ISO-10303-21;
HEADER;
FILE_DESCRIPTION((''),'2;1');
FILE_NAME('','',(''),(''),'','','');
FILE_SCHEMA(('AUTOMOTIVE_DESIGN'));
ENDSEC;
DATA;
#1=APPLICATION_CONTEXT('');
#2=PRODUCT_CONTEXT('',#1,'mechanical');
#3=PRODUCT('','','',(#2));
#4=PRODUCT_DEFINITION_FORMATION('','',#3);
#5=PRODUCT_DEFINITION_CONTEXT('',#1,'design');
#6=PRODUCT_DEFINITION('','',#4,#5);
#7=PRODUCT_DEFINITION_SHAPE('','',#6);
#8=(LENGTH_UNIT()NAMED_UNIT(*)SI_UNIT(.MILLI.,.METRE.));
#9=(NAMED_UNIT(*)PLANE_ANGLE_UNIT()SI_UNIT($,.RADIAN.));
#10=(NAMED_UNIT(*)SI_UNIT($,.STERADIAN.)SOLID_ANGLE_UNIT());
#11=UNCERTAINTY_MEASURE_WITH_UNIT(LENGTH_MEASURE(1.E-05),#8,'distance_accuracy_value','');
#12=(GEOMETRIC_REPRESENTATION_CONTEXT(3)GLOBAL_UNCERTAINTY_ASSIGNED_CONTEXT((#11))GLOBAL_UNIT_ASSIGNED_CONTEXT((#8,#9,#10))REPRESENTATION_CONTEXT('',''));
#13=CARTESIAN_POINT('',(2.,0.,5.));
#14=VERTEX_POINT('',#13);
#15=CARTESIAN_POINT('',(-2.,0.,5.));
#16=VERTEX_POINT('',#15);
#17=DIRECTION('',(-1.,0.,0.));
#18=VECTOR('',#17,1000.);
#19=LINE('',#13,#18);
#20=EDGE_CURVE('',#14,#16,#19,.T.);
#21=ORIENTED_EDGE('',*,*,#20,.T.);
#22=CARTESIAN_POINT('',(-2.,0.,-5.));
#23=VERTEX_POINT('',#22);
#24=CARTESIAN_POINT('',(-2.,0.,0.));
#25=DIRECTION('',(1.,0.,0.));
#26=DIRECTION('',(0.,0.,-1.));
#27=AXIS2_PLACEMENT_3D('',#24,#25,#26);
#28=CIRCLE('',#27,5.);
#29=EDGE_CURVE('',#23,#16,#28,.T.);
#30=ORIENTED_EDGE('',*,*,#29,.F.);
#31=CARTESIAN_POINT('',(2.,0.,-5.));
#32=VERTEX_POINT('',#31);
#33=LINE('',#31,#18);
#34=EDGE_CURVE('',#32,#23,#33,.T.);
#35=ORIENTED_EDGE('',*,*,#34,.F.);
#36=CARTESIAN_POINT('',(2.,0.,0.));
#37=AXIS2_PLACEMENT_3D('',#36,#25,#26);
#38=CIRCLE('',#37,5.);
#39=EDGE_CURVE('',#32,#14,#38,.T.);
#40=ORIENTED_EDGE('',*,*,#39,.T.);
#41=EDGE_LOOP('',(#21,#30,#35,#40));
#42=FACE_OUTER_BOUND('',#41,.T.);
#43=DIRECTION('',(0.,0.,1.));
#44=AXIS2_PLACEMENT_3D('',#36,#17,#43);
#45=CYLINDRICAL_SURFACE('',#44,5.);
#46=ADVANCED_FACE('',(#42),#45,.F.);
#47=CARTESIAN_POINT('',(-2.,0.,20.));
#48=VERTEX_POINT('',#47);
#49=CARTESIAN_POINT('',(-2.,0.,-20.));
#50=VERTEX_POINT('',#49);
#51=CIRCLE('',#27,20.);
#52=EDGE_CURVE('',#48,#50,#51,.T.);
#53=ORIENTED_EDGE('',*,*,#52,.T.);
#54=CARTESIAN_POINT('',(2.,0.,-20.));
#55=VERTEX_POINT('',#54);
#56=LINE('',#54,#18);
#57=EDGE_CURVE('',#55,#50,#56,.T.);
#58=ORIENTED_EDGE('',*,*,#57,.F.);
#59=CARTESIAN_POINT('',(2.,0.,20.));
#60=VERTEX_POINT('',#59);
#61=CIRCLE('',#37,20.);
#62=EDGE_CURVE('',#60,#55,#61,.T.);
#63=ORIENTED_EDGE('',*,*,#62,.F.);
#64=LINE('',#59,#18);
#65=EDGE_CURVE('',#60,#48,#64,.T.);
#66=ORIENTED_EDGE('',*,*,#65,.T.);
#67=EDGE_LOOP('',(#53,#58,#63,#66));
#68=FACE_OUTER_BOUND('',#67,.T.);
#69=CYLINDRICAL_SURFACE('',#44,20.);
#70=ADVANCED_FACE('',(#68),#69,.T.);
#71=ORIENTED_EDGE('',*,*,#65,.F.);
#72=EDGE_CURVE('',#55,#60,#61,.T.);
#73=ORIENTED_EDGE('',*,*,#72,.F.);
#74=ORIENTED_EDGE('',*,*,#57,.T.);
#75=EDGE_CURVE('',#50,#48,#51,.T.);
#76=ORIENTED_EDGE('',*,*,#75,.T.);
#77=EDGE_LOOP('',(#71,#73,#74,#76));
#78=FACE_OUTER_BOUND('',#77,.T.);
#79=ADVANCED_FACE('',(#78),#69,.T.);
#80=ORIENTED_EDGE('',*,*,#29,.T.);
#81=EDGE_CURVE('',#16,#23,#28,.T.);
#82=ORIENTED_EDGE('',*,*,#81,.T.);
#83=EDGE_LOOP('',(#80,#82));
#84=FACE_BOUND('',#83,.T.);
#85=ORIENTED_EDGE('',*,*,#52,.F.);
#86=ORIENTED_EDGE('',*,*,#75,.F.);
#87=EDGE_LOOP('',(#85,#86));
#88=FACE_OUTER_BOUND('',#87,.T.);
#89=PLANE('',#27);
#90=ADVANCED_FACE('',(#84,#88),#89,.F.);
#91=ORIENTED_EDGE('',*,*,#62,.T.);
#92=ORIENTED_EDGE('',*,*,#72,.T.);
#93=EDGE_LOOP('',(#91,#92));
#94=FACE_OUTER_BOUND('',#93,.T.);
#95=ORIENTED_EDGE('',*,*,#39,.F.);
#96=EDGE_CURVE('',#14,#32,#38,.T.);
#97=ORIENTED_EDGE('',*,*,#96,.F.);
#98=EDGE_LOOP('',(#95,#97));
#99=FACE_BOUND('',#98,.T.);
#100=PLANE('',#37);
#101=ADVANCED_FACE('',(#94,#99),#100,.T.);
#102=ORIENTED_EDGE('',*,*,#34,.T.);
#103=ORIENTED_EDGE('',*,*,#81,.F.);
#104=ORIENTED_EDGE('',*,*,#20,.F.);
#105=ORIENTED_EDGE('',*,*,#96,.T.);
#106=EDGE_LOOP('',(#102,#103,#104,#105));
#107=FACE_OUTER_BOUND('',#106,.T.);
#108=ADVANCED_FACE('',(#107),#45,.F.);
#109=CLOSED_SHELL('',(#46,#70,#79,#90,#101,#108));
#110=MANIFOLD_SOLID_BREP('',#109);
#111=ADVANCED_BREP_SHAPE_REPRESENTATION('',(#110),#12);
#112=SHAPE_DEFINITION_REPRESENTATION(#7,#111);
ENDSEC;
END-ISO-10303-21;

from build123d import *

# Parameters (mm, degrees)
SKETCH1_R           = 20
SKETCH1_R_2         = 5
BOSS_EXTRUDE1_DEPTH = 2


with BuildPart() as part:
    # Sketch1 → Boss-Extrude1 (new, symmetric)
    with BuildSketch(Plane(origin=(0, 0, 0), x_dir=(0, 0, -1), z_dir=(1, 0, 0))):
        Circle(SKETCH1_R)
        Circle(SKETCH1_R_2, mode=Mode.SUBTRACT)
    extrude(amount=BOSS_EXTRUDE1_DEPTH, both=True)


solid = part.part
